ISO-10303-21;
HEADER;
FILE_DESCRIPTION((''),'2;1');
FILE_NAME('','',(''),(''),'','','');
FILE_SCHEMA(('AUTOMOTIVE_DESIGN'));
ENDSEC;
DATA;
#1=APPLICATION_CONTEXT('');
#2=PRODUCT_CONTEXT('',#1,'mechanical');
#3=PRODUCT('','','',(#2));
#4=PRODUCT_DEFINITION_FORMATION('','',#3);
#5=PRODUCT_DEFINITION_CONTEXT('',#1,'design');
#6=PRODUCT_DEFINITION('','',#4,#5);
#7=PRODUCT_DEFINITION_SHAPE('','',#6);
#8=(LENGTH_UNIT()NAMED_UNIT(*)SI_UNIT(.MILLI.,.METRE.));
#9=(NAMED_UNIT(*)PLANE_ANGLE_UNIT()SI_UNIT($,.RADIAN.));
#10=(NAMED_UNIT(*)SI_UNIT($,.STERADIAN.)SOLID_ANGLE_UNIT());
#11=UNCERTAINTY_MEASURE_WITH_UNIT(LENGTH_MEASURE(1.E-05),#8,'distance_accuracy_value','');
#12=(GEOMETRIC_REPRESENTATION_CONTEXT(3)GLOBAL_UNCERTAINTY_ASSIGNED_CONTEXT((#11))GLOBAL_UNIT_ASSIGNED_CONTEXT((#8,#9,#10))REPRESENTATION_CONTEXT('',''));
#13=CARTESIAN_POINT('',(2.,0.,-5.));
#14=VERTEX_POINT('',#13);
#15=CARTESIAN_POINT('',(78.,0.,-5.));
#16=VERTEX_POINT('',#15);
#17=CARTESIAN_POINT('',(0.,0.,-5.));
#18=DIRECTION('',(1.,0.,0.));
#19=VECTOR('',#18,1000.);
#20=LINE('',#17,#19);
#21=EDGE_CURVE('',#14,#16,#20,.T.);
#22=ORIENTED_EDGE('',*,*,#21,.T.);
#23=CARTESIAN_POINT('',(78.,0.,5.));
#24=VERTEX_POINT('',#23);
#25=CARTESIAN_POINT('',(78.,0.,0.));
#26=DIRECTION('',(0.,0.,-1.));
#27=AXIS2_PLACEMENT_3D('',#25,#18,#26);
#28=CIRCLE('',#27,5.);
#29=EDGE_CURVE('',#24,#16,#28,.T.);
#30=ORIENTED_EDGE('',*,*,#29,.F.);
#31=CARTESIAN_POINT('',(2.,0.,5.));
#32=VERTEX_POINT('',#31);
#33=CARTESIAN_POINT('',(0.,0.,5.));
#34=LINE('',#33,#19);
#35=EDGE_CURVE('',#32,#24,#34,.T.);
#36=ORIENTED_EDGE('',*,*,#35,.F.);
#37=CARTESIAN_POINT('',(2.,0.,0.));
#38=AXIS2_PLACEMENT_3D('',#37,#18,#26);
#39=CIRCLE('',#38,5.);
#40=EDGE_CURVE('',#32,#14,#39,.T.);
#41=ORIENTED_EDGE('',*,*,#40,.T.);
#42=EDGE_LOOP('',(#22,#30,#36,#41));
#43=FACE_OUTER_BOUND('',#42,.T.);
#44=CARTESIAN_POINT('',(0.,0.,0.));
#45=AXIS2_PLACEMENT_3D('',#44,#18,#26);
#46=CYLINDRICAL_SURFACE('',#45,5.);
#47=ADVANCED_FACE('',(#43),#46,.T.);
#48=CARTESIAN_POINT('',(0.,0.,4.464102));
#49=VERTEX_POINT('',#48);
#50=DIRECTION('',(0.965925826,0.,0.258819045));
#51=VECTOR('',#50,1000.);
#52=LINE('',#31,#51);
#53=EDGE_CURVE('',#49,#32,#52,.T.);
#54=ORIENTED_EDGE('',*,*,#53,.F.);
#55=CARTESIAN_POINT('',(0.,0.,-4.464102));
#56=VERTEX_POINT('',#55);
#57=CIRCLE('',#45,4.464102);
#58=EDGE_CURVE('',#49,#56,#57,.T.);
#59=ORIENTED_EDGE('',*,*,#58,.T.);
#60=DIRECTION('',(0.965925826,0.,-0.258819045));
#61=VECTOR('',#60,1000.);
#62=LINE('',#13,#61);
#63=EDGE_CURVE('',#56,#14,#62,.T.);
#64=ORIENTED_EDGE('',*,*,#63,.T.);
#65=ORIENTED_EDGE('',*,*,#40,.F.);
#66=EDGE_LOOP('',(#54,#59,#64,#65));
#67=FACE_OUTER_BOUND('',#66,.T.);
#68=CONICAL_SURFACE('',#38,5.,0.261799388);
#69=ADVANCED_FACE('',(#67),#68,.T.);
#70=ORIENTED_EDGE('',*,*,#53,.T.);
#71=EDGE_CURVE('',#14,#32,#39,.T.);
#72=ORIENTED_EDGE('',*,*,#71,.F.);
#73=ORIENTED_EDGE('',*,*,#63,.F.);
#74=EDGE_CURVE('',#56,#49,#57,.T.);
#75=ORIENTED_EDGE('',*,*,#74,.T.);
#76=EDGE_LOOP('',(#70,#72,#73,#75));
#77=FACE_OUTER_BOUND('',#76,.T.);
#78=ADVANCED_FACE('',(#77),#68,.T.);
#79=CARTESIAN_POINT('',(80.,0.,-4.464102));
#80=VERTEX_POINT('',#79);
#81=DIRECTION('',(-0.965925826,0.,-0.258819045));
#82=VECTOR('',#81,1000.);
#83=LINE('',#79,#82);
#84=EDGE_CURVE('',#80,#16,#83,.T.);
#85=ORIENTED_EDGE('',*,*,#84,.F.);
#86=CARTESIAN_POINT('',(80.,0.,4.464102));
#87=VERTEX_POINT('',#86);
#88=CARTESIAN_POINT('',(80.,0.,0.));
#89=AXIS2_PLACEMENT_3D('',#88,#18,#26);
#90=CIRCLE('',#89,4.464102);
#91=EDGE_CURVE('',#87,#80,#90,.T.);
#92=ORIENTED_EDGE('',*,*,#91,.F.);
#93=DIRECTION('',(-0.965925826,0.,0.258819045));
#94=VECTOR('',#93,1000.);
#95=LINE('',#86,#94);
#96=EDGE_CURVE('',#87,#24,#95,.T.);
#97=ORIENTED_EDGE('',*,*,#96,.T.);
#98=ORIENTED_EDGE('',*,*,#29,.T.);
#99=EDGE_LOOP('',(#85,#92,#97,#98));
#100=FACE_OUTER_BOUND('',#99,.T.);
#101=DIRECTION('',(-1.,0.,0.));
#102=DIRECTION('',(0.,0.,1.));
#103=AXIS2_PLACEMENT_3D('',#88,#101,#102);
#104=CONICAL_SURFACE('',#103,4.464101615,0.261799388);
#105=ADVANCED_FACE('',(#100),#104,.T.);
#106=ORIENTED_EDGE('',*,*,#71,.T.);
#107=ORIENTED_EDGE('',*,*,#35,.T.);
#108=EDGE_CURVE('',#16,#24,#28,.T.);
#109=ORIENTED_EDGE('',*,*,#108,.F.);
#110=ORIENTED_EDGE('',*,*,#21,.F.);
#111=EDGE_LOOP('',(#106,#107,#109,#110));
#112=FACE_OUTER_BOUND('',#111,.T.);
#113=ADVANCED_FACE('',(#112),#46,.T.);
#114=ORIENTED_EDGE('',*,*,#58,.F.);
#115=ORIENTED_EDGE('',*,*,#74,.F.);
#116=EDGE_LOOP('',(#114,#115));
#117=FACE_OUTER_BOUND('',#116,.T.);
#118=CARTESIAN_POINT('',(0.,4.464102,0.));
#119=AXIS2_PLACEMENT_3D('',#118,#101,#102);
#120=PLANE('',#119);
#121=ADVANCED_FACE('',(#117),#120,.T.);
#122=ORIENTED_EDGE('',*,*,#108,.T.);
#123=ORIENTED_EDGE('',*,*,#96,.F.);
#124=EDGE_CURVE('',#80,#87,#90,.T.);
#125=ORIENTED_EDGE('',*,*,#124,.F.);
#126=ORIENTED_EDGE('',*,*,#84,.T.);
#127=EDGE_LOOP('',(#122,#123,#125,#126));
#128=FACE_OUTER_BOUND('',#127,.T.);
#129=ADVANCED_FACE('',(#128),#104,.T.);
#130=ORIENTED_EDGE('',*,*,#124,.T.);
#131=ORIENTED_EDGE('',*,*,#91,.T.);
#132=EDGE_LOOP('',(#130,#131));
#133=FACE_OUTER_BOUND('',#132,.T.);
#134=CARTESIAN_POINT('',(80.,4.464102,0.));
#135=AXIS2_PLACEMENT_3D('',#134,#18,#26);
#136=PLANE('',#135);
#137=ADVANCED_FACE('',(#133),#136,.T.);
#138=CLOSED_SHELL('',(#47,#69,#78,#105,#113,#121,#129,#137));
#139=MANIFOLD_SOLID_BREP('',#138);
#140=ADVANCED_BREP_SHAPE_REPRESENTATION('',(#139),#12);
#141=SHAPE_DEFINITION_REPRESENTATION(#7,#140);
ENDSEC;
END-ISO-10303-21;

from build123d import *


with BuildPart() as part:
    # Dimensioned Sketch → Base-Revolve (revolve)
    with BuildSketch(Plane.XY, mode=Mode.PRIVATE) as base_revolve_sk:
        Polygon((0, 0), (80, 0), (80, 4.464101615), (78, 5), (2, 5), (0, 4.464101615), align=None)
    revolve(base_revolve_sk.sketch.rotate(Axis((0, 0, 0), (-1, 0, 0)), 90), axis=Axis((0, 0, 0), (-1, 0, 0)))


solid = part.part
